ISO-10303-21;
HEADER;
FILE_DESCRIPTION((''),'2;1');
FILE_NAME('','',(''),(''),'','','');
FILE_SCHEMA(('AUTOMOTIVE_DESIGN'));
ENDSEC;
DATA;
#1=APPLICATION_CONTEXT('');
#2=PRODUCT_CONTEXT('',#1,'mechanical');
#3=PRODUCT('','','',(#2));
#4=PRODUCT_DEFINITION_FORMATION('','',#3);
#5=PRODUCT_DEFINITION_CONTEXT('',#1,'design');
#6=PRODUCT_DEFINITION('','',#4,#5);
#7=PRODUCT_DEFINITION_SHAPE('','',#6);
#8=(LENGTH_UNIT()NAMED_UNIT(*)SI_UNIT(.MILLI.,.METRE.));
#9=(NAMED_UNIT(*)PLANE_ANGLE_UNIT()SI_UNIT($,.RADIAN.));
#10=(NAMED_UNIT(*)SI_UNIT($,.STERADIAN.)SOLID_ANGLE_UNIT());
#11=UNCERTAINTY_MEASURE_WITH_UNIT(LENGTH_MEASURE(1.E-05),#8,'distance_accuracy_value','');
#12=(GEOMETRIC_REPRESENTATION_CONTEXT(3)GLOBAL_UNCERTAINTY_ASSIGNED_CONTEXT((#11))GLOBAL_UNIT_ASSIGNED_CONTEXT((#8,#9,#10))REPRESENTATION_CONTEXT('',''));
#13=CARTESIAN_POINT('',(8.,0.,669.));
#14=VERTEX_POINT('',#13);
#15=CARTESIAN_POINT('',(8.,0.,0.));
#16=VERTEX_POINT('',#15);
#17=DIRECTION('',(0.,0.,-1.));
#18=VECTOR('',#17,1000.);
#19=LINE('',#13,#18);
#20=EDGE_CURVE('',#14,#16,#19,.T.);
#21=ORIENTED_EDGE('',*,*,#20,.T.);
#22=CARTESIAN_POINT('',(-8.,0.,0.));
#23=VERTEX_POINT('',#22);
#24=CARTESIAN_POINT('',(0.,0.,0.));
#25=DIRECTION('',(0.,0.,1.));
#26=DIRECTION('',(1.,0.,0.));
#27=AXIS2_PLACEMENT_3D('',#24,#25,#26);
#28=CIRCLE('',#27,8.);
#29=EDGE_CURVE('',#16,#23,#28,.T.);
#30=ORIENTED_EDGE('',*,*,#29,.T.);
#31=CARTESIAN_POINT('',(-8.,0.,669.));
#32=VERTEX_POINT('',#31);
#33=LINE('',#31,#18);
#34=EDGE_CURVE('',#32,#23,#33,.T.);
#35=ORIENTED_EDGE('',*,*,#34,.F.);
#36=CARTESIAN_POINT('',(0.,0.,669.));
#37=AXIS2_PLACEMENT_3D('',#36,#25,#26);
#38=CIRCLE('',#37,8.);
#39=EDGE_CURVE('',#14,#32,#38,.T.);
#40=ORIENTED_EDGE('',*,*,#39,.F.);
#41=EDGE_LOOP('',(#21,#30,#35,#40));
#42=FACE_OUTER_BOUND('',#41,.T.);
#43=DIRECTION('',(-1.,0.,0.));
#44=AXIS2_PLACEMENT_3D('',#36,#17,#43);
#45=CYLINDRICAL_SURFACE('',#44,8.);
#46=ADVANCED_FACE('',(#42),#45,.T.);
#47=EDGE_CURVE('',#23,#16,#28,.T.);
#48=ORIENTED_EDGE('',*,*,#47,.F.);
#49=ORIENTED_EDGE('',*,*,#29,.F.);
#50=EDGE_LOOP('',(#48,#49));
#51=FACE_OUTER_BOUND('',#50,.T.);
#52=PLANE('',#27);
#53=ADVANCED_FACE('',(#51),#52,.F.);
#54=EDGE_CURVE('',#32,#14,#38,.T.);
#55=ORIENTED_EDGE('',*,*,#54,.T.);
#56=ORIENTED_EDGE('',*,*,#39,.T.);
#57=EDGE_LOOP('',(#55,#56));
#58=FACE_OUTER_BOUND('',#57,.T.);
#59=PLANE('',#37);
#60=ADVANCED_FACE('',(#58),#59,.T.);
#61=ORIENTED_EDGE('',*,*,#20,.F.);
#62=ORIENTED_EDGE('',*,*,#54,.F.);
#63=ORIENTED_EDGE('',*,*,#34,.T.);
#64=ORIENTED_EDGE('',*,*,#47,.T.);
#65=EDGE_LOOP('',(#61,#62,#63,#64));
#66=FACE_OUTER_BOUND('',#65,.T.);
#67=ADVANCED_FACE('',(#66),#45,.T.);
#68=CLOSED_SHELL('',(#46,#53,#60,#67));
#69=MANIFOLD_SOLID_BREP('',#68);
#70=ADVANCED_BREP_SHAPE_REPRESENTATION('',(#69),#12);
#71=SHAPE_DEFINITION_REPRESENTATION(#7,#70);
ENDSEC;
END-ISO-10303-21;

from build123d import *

# Parameters (mm, degrees)
SKETCH1_R           = 8
BOSS_EXTRUDE1_DEPTH = 669


with BuildPart() as part:
    # Sketch1 → Boss-Extrude1 (new body)
    with BuildSketch(Plane.XY):
        Circle(SKETCH1_R)
    extrude(amount=BOSS_EXTRUDE1_DEPTH)


solid = part.part
